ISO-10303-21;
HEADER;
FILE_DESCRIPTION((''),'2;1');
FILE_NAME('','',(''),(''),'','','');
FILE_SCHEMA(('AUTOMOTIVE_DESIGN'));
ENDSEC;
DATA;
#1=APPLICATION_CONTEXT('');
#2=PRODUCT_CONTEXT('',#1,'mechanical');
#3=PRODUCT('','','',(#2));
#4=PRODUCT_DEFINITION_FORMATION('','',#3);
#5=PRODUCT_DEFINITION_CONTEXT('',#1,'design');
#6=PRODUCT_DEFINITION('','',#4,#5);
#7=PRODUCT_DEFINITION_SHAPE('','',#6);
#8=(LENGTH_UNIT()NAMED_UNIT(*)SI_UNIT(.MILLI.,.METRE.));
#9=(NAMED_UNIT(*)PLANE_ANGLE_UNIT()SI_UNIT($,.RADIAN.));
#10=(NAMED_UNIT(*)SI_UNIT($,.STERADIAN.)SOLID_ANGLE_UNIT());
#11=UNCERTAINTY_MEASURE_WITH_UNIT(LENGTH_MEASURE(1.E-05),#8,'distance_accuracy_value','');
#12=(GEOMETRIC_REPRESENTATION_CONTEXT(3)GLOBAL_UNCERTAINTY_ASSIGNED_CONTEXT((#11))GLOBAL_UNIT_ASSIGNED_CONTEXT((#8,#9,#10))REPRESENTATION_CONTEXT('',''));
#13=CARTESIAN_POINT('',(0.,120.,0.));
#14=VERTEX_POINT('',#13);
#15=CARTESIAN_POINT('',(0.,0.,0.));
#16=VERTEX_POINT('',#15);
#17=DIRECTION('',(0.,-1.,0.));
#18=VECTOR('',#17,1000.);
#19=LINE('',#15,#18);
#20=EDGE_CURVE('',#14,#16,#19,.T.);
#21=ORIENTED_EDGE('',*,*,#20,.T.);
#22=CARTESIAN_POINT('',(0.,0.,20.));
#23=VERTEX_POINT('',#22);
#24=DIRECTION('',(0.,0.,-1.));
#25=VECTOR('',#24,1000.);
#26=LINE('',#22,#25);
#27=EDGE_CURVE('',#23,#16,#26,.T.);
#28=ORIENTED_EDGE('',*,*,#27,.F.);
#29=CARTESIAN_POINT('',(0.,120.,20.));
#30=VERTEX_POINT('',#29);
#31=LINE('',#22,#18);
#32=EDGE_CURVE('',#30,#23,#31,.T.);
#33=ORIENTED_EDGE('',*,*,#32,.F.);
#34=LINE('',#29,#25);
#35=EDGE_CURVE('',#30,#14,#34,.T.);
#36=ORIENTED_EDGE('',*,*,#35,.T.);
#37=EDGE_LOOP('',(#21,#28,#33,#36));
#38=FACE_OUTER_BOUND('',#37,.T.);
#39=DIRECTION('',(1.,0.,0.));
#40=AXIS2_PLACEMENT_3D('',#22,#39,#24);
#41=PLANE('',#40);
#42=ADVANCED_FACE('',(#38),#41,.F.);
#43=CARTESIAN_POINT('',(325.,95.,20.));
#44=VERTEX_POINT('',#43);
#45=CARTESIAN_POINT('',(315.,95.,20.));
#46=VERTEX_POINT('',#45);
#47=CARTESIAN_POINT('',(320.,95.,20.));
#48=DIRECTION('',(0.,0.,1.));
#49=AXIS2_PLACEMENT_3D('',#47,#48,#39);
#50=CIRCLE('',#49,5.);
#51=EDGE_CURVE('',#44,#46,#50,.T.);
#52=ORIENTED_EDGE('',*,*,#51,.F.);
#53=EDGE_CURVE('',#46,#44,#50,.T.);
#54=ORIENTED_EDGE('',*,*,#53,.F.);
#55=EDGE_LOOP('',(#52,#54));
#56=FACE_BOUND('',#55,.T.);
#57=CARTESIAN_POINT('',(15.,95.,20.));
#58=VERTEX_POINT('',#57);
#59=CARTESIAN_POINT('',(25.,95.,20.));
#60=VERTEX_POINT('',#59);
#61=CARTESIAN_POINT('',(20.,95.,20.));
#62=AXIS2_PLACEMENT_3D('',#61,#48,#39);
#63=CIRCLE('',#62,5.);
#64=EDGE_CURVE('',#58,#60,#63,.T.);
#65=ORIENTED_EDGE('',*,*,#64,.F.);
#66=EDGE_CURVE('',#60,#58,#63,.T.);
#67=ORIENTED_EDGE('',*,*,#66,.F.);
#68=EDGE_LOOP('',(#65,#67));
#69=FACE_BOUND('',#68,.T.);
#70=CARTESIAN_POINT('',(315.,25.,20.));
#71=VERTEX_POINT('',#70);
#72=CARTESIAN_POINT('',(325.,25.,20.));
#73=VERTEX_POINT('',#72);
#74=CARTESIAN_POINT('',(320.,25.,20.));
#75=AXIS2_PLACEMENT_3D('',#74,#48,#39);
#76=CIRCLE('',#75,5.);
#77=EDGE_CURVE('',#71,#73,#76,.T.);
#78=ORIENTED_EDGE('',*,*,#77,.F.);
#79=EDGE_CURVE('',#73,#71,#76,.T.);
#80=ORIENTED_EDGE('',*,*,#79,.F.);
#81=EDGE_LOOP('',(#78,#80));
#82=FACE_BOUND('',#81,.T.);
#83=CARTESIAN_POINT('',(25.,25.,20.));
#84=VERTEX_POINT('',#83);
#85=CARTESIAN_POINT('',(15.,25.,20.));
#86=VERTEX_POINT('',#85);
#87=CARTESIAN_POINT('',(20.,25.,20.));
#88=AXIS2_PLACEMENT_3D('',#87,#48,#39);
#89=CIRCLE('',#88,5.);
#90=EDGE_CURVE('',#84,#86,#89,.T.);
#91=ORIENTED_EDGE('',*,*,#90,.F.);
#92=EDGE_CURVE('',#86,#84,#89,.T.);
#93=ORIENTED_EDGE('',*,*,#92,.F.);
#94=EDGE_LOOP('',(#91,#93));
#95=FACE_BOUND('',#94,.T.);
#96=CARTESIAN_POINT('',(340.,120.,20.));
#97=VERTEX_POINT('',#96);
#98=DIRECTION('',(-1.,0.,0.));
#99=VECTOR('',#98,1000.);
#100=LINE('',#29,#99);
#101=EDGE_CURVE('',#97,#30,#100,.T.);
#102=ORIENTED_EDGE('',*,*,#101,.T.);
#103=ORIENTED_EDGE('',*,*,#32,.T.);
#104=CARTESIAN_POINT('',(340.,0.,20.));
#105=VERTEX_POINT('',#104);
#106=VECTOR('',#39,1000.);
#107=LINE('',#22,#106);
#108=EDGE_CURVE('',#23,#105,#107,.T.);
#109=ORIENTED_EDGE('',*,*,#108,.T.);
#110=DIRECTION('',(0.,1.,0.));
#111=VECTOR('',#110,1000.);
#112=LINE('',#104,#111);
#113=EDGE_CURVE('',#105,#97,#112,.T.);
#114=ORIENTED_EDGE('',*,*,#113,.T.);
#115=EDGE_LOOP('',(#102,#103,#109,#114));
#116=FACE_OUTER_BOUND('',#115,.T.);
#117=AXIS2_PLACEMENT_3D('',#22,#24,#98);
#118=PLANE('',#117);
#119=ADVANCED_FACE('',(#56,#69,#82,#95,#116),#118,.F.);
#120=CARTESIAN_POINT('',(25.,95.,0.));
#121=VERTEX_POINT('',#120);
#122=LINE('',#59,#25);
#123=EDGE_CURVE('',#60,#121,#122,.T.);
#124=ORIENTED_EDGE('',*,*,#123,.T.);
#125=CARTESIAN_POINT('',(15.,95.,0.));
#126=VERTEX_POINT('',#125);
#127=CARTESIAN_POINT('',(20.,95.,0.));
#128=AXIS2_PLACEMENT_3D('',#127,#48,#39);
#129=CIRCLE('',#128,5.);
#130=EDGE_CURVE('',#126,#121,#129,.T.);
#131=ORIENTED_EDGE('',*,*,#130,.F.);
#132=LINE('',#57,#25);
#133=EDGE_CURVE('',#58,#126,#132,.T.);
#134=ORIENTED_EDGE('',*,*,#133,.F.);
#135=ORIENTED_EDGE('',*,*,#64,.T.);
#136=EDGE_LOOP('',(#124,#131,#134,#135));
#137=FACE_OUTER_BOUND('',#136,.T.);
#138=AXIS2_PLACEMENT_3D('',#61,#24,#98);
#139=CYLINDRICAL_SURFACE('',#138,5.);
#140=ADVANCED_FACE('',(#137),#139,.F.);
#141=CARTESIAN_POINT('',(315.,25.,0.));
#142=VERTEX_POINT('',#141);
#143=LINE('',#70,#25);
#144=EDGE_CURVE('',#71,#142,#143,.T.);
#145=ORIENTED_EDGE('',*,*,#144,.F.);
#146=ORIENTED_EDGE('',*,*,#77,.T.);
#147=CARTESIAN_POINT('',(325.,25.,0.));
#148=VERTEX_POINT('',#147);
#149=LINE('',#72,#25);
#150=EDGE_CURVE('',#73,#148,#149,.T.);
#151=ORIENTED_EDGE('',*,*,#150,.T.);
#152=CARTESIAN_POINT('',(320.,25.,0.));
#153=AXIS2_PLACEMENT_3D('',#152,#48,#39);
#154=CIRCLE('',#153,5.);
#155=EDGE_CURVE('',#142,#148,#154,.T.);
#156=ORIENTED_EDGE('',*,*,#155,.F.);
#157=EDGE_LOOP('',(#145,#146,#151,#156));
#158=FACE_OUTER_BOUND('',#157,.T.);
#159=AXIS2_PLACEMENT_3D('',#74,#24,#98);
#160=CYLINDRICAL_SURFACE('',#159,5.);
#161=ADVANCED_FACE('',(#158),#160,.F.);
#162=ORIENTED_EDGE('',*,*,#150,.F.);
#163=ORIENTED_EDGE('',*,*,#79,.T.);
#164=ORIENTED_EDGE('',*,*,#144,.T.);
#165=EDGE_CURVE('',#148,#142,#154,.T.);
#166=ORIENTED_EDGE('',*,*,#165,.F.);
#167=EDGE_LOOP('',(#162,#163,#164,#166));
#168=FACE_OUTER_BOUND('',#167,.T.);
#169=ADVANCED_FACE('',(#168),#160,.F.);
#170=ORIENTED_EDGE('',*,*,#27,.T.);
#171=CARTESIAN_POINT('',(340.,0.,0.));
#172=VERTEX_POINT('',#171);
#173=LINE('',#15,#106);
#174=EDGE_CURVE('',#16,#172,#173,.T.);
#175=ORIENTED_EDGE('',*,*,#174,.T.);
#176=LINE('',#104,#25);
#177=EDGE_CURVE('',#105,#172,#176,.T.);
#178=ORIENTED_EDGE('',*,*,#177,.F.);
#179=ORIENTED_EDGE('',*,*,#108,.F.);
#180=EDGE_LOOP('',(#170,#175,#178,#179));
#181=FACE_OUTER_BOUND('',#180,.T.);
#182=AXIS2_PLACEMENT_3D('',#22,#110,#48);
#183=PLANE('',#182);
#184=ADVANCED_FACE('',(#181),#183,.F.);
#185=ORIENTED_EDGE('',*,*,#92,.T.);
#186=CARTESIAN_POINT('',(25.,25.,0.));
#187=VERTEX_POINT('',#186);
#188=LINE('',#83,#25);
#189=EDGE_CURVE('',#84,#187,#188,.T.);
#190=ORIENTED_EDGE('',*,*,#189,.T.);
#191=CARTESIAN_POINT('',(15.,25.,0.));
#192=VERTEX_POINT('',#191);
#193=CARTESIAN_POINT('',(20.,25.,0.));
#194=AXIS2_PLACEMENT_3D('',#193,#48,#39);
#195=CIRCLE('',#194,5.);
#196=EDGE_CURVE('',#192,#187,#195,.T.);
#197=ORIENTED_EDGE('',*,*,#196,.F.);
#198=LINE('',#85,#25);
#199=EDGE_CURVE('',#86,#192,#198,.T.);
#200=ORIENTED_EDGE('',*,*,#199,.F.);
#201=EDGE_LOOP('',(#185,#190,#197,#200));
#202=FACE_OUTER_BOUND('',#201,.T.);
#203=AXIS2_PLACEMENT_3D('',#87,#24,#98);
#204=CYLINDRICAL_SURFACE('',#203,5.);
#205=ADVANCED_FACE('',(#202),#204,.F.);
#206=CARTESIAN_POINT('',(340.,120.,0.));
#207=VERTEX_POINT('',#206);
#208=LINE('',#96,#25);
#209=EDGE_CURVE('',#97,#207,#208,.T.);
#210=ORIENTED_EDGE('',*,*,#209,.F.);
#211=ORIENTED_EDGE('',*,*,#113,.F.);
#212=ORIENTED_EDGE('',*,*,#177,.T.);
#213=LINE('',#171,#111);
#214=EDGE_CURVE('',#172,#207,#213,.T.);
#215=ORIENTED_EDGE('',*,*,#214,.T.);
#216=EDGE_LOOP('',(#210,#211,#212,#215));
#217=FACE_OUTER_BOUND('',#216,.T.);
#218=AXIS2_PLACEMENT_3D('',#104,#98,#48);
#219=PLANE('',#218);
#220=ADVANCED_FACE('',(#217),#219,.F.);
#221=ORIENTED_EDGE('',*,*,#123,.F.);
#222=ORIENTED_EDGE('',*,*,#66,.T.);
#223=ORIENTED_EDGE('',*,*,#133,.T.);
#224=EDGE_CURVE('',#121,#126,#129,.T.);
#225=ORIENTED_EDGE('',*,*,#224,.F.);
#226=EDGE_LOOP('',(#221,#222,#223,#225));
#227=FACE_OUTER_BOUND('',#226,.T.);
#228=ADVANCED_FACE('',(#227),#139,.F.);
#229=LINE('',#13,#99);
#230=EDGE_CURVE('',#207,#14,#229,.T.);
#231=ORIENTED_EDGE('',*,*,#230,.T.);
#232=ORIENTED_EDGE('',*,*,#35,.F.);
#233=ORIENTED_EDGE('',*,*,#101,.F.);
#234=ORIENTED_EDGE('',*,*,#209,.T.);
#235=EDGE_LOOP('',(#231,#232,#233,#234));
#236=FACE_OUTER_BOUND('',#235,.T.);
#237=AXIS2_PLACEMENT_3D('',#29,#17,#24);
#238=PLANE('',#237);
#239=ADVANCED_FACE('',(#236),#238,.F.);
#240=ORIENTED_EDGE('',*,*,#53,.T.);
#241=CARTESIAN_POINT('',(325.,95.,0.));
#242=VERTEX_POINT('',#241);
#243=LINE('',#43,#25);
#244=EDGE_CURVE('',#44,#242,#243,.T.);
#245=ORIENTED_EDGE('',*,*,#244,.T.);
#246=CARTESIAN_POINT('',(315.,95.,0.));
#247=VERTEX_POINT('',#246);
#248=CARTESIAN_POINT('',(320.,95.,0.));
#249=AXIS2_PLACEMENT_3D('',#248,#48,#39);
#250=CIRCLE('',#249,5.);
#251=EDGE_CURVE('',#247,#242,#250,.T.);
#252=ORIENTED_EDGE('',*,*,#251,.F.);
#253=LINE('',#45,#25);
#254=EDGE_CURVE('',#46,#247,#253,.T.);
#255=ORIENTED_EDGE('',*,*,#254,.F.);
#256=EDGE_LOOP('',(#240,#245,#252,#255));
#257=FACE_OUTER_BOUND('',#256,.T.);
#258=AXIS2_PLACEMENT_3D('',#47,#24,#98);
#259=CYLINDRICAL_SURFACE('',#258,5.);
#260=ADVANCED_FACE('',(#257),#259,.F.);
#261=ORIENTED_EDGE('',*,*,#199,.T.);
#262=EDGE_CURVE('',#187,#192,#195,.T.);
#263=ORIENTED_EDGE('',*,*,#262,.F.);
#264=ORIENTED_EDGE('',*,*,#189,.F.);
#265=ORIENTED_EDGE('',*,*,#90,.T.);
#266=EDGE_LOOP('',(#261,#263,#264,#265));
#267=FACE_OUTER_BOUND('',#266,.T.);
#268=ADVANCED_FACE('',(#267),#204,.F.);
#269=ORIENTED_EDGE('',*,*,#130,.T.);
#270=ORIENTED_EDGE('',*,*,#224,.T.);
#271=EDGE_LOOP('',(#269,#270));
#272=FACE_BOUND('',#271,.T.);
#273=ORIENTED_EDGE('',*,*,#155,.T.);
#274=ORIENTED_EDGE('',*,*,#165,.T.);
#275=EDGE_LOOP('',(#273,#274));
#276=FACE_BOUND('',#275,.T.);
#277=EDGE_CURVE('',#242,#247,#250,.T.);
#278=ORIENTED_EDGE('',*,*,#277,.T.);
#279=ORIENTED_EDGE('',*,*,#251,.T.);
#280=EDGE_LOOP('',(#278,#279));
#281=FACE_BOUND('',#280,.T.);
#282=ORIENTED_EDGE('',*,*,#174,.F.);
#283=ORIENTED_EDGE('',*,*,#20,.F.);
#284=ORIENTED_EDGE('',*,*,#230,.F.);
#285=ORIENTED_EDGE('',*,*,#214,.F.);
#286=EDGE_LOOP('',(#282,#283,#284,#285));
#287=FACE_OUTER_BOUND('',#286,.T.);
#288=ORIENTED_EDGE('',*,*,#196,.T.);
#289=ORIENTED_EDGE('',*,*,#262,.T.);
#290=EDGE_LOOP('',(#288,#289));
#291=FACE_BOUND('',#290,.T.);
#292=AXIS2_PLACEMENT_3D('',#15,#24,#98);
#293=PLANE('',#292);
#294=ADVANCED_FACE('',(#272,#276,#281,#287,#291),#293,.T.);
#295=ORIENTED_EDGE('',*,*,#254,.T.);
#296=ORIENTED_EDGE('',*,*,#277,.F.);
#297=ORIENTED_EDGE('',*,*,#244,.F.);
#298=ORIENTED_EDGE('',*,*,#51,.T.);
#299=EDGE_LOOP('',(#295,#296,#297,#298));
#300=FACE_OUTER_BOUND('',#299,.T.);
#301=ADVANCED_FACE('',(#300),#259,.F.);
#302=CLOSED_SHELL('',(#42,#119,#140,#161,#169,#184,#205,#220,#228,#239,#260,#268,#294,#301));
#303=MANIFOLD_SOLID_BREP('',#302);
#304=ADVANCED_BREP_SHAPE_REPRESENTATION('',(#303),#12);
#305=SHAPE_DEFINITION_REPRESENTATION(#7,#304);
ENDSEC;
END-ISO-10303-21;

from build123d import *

# Parameters (mm, degrees)
SKETCH1_W           = 340
SKETCH1_H           = 120
SKETCH1_R           = 5
BOSS_EXTRUDE1_DEPTH = 20


with BuildPart() as part:
    # Sketch1 → Boss-Extrude1 (new body)
    with BuildSketch(Plane.XY):
        with Locations((170, 60)):
            Rectangle(SKETCH1_W, SKETCH1_H)
        with Locations((20, 95)):
            Circle(SKETCH1_R, mode=Mode.SUBTRACT)
        with Locations((320, 95)):
            Circle(SKETCH1_R, mode=Mode.SUBTRACT)
        with Locations((320, 25)):
            Circle(SKETCH1_R, mode=Mode.SUBTRACT)
        with Locations((20, 25)):
            Circle(SKETCH1_R, mode=Mode.SUBTRACT)
    extrude(amount=BOSS_EXTRUDE1_DEPTH)


solid = part.part
